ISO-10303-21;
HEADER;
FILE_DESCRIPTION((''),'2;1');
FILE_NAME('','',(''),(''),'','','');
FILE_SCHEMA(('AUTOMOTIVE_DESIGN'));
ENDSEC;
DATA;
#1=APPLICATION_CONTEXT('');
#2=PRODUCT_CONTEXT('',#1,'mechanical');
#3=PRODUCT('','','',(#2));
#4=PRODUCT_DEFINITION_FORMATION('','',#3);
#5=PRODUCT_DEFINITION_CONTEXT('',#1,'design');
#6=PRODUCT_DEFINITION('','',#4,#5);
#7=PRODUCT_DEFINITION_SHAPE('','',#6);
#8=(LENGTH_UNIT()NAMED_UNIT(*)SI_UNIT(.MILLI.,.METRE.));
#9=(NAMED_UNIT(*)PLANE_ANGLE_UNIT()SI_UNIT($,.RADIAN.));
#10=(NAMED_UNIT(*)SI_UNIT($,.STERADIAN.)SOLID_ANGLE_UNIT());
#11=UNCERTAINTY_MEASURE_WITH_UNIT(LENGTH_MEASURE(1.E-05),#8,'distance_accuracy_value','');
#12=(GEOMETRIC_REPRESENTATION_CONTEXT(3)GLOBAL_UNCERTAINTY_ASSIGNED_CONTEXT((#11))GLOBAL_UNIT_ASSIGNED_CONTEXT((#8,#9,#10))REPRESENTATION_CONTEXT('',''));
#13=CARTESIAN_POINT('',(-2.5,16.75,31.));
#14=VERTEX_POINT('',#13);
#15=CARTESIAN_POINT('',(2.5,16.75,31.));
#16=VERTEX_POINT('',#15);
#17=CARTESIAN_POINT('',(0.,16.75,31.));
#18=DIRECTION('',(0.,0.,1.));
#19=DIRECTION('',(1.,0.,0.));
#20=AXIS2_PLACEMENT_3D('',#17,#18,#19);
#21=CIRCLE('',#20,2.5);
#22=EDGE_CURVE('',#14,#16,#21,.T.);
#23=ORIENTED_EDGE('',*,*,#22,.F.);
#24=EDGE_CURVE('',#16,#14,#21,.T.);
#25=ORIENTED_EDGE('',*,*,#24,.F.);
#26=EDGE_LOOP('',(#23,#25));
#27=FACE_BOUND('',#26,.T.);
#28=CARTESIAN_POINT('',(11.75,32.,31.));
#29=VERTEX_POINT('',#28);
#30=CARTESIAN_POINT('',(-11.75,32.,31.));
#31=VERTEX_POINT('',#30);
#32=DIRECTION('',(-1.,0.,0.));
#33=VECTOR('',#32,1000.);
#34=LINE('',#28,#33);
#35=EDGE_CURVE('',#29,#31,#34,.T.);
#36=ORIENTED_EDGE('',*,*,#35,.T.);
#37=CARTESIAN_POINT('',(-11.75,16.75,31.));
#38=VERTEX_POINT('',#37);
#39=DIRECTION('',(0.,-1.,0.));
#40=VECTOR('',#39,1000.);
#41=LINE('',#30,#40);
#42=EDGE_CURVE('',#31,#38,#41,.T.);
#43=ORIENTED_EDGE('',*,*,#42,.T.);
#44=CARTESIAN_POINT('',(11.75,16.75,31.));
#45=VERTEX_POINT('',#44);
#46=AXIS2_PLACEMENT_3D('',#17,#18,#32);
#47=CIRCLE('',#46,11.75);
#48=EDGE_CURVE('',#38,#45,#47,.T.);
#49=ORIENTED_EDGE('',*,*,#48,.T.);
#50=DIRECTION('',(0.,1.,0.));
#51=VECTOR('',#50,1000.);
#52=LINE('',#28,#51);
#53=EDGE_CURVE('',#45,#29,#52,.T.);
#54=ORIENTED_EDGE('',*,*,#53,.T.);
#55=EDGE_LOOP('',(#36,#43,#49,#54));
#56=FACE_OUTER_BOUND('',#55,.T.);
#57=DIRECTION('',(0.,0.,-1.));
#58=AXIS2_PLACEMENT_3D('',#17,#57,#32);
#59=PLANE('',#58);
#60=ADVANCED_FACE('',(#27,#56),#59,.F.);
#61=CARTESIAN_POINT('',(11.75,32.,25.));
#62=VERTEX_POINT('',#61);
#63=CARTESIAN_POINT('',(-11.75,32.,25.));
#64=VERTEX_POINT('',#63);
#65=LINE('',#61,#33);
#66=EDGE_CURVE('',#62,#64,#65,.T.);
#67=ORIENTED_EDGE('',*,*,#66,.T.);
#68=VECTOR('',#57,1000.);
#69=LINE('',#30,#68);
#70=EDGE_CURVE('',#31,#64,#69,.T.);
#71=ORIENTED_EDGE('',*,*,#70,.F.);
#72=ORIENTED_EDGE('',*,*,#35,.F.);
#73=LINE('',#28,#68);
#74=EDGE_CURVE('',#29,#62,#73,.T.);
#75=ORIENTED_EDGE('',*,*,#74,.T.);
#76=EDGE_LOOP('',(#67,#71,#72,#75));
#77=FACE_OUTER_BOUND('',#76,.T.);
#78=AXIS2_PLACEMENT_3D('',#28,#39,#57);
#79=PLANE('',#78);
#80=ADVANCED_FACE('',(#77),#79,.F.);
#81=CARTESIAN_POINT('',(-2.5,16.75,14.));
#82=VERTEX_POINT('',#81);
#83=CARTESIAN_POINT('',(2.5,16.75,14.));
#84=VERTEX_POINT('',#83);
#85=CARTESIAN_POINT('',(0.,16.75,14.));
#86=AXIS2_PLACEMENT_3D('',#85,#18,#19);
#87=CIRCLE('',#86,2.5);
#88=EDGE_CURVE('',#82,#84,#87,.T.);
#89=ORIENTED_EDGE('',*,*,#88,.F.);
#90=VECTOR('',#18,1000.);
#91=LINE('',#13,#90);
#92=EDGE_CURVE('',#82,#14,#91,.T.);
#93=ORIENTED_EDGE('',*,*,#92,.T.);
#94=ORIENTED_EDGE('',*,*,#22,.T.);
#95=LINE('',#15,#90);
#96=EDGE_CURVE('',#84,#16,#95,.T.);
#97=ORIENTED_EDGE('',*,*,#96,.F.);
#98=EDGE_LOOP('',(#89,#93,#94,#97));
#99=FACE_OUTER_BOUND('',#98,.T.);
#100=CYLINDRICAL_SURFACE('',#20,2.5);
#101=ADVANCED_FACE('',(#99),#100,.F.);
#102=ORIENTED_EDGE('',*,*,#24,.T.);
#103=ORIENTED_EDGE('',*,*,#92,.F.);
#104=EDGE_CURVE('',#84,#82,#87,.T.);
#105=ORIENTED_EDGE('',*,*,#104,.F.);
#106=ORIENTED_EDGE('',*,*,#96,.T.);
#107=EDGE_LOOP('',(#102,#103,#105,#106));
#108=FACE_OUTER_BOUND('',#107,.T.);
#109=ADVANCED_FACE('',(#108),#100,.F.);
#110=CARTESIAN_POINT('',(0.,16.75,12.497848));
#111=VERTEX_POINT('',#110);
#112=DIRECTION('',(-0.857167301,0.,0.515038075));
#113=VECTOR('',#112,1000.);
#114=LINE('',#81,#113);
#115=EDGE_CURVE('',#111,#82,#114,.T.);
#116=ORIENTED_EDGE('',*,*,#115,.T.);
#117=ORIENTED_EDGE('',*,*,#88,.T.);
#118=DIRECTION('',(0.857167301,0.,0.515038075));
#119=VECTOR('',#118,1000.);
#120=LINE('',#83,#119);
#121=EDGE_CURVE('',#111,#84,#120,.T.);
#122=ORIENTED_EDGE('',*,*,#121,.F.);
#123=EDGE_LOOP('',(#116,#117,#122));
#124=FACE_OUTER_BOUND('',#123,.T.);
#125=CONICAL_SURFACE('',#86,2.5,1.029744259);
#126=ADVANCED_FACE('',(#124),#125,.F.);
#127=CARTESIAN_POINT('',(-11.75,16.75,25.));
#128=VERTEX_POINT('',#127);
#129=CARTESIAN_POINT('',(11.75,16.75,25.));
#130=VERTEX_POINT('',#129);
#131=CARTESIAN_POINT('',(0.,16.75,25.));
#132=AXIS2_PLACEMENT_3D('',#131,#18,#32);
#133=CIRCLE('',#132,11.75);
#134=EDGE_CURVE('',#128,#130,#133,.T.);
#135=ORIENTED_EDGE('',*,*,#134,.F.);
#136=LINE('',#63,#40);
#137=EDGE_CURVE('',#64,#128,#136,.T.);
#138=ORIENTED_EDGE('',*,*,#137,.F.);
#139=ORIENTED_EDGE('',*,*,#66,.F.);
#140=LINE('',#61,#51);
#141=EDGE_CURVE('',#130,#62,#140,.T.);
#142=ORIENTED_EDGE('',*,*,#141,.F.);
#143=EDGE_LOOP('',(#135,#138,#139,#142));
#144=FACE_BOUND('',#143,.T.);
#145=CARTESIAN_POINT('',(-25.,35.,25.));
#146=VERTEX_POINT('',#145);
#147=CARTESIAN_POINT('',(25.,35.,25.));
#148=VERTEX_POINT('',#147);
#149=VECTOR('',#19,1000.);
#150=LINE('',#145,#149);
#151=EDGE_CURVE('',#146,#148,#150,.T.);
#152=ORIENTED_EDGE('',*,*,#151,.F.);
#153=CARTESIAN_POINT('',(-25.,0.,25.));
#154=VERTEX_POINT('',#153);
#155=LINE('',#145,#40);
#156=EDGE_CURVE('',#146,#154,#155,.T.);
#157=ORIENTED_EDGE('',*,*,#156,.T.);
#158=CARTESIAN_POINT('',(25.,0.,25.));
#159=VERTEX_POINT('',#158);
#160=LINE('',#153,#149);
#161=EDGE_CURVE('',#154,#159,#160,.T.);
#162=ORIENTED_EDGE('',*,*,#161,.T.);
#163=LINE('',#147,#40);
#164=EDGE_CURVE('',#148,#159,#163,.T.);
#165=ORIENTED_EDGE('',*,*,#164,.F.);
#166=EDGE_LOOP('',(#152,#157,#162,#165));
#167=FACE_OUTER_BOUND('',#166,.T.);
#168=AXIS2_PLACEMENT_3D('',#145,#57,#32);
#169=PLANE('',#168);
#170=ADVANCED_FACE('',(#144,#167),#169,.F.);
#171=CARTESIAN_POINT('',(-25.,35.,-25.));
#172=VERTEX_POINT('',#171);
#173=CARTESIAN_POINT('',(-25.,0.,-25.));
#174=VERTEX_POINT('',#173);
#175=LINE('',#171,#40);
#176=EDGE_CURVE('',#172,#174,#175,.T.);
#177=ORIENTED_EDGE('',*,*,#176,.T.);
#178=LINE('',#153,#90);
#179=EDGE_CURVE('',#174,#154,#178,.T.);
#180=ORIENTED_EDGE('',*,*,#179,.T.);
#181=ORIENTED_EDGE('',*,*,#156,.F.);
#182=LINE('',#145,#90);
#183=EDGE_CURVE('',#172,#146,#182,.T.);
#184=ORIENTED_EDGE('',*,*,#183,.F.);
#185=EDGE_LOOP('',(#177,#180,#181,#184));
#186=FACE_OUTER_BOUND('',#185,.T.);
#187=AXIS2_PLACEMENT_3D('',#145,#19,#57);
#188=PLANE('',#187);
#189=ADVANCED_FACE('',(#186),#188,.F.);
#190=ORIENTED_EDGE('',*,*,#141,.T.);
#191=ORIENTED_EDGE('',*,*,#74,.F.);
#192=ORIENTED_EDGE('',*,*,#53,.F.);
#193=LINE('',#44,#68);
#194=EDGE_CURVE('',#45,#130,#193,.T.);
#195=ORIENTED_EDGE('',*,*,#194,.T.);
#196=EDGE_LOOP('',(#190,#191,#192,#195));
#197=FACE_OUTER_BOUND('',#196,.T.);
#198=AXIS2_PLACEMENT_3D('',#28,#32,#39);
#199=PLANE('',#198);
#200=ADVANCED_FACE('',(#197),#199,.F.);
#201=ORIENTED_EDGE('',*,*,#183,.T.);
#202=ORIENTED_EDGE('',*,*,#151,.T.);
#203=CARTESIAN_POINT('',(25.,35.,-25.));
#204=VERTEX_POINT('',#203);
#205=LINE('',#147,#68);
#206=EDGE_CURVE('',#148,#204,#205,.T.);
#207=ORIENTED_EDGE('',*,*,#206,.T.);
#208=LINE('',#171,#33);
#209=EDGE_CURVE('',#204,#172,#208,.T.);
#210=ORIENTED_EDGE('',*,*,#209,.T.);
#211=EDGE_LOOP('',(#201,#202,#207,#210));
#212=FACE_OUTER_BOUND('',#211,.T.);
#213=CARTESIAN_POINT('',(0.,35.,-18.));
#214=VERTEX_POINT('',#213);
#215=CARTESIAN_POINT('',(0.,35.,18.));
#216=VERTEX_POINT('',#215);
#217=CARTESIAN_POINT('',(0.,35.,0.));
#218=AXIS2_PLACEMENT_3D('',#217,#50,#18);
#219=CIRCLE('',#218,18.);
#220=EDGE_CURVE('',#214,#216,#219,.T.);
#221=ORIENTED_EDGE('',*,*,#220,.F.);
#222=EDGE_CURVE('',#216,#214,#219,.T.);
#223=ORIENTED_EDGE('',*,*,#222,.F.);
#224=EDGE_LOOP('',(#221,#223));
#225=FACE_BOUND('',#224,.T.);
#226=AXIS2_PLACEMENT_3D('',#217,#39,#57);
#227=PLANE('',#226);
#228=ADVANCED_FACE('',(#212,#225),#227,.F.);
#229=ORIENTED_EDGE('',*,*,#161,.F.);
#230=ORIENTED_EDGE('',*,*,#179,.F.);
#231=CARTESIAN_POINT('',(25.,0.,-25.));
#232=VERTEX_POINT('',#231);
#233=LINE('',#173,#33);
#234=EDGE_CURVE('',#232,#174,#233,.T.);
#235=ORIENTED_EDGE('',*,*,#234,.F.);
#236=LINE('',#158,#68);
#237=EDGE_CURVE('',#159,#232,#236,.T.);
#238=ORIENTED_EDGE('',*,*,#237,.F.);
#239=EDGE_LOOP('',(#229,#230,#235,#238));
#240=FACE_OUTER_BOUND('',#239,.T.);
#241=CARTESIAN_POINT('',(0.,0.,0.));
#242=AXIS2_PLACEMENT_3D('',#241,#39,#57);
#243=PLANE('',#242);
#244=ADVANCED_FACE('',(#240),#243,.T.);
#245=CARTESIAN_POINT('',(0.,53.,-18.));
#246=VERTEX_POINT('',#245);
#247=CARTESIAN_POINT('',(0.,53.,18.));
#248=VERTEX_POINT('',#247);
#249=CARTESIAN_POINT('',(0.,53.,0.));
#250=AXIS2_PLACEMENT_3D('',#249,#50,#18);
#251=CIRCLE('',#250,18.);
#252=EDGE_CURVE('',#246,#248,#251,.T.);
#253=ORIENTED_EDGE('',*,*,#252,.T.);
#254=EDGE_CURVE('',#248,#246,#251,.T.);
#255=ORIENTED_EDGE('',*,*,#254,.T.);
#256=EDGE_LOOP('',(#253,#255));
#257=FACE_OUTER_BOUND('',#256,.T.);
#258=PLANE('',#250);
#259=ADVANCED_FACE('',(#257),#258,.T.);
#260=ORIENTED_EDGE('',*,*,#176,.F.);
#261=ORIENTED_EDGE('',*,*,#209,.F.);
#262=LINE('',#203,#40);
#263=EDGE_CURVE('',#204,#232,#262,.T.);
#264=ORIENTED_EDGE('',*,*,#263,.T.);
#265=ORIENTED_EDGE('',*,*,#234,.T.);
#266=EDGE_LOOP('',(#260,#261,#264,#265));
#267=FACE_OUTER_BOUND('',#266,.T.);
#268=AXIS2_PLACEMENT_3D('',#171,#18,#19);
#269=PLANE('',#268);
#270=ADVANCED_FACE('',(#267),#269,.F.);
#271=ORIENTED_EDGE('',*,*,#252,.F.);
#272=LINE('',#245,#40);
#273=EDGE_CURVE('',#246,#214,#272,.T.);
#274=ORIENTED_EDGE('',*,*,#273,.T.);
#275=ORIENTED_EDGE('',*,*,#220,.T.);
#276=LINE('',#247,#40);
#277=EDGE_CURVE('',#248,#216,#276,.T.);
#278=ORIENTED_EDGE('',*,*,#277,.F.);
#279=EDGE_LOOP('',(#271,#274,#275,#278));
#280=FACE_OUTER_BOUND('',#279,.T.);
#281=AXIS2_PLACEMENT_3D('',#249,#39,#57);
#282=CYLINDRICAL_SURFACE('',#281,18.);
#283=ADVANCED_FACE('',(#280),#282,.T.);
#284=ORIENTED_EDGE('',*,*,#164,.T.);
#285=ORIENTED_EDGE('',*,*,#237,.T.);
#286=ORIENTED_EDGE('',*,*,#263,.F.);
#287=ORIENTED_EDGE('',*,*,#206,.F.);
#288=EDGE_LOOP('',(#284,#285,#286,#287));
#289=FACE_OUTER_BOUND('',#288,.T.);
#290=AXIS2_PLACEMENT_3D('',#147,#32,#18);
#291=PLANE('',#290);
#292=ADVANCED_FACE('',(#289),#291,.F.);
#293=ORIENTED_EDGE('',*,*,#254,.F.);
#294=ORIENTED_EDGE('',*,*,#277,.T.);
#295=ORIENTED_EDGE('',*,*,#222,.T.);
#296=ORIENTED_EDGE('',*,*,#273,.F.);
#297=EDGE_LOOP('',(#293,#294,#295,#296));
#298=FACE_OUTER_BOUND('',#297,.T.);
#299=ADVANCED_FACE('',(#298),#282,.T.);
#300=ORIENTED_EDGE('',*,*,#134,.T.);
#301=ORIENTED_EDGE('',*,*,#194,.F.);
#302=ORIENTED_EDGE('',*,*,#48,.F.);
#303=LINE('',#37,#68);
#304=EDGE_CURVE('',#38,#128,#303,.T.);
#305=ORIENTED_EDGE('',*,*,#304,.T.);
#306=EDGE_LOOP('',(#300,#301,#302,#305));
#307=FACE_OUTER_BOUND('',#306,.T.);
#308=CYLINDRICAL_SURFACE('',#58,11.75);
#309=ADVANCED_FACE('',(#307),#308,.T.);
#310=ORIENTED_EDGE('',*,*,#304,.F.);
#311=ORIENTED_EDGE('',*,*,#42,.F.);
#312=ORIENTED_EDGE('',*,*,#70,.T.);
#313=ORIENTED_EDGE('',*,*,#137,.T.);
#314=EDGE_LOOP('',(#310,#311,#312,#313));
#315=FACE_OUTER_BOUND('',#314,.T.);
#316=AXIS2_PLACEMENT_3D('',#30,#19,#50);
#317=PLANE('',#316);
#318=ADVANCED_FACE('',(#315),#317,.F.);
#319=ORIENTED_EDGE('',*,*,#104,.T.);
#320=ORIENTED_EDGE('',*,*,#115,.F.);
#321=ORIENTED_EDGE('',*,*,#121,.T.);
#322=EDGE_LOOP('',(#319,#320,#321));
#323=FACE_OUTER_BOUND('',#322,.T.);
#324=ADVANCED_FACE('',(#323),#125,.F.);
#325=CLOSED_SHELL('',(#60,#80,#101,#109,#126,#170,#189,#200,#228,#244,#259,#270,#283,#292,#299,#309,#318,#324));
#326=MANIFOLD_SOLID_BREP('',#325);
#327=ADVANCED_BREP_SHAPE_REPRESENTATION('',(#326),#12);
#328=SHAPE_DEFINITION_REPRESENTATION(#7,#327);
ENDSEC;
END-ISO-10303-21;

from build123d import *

# Parameters (mm, degrees)
SKETCH1_W             = 50
SKETCH1_H             = 50
BOSS_EXTRUDE1_DEPTH   = 35
SKETCH2_R             = 18
BOSS_EXTRUDE2_DEPTH   = 18
BOSS_EXTRUDE3_DEPTH   = 6
M6_TAPPED_HOLE1_D     = 5
M6_TAPPED_HOLE1_DEPTH = 17
M6_TAPPED_HOLE1_TIP   = 1.502151548


with BuildPart() as part:
    # Sketch1 → Boss-Extrude1 (new body)
    with BuildSketch(Plane(origin=(0, 0, 0), x_dir=(1, 0, 0), z_dir=(0, 1, 0))):
        Rectangle(SKETCH1_W, SKETCH1_H)
    extrude(amount=BOSS_EXTRUDE1_DEPTH)

    # Sketch2 → Boss-Extrude2 (add)
    with BuildSketch(Plane(origin=(0, 35, 0), x_dir=(1, 0, 0), z_dir=(0, 1, 0))):
        with Locations(Location((0, 0, 0), (0, 0, 270))):
            Circle(SKETCH2_R)
    extrude(amount=BOSS_EXTRUDE2_DEPTH)

    # Sketch3 → Boss-Extrude3 (add)
    with BuildSketch(Plane.XY.offset(25)):
        with BuildLine():
            Line((11.75, 32), (-11.75, 32))
            Line((-11.75, 32), (-11.75, 16.75))
            ThreePointArc((-11.75, 16.75), (0, 5), (11.75, 16.75))
            Line((11.75, 16.75), (11.75, 32))
        make_face()
    extrude(amount=BOSS_EXTRUDE3_DEPTH)

    # M6 Tapped Hole1
    with Locations(Plane.XY.offset(31)):
        with Locations((0, 16.75)):
            Hole(M6_TAPPED_HOLE1_D / 2, depth=M6_TAPPED_HOLE1_DEPTH)
            with Locations((0, 0, -(M6_TAPPED_HOLE1_DEPTH + M6_TAPPED_HOLE1_TIP / 2))):  # 118° drill point
                Cone(0, M6_TAPPED_HOLE1_D / 2, M6_TAPPED_HOLE1_TIP, mode=Mode.SUBTRACT)


solid = part.part
